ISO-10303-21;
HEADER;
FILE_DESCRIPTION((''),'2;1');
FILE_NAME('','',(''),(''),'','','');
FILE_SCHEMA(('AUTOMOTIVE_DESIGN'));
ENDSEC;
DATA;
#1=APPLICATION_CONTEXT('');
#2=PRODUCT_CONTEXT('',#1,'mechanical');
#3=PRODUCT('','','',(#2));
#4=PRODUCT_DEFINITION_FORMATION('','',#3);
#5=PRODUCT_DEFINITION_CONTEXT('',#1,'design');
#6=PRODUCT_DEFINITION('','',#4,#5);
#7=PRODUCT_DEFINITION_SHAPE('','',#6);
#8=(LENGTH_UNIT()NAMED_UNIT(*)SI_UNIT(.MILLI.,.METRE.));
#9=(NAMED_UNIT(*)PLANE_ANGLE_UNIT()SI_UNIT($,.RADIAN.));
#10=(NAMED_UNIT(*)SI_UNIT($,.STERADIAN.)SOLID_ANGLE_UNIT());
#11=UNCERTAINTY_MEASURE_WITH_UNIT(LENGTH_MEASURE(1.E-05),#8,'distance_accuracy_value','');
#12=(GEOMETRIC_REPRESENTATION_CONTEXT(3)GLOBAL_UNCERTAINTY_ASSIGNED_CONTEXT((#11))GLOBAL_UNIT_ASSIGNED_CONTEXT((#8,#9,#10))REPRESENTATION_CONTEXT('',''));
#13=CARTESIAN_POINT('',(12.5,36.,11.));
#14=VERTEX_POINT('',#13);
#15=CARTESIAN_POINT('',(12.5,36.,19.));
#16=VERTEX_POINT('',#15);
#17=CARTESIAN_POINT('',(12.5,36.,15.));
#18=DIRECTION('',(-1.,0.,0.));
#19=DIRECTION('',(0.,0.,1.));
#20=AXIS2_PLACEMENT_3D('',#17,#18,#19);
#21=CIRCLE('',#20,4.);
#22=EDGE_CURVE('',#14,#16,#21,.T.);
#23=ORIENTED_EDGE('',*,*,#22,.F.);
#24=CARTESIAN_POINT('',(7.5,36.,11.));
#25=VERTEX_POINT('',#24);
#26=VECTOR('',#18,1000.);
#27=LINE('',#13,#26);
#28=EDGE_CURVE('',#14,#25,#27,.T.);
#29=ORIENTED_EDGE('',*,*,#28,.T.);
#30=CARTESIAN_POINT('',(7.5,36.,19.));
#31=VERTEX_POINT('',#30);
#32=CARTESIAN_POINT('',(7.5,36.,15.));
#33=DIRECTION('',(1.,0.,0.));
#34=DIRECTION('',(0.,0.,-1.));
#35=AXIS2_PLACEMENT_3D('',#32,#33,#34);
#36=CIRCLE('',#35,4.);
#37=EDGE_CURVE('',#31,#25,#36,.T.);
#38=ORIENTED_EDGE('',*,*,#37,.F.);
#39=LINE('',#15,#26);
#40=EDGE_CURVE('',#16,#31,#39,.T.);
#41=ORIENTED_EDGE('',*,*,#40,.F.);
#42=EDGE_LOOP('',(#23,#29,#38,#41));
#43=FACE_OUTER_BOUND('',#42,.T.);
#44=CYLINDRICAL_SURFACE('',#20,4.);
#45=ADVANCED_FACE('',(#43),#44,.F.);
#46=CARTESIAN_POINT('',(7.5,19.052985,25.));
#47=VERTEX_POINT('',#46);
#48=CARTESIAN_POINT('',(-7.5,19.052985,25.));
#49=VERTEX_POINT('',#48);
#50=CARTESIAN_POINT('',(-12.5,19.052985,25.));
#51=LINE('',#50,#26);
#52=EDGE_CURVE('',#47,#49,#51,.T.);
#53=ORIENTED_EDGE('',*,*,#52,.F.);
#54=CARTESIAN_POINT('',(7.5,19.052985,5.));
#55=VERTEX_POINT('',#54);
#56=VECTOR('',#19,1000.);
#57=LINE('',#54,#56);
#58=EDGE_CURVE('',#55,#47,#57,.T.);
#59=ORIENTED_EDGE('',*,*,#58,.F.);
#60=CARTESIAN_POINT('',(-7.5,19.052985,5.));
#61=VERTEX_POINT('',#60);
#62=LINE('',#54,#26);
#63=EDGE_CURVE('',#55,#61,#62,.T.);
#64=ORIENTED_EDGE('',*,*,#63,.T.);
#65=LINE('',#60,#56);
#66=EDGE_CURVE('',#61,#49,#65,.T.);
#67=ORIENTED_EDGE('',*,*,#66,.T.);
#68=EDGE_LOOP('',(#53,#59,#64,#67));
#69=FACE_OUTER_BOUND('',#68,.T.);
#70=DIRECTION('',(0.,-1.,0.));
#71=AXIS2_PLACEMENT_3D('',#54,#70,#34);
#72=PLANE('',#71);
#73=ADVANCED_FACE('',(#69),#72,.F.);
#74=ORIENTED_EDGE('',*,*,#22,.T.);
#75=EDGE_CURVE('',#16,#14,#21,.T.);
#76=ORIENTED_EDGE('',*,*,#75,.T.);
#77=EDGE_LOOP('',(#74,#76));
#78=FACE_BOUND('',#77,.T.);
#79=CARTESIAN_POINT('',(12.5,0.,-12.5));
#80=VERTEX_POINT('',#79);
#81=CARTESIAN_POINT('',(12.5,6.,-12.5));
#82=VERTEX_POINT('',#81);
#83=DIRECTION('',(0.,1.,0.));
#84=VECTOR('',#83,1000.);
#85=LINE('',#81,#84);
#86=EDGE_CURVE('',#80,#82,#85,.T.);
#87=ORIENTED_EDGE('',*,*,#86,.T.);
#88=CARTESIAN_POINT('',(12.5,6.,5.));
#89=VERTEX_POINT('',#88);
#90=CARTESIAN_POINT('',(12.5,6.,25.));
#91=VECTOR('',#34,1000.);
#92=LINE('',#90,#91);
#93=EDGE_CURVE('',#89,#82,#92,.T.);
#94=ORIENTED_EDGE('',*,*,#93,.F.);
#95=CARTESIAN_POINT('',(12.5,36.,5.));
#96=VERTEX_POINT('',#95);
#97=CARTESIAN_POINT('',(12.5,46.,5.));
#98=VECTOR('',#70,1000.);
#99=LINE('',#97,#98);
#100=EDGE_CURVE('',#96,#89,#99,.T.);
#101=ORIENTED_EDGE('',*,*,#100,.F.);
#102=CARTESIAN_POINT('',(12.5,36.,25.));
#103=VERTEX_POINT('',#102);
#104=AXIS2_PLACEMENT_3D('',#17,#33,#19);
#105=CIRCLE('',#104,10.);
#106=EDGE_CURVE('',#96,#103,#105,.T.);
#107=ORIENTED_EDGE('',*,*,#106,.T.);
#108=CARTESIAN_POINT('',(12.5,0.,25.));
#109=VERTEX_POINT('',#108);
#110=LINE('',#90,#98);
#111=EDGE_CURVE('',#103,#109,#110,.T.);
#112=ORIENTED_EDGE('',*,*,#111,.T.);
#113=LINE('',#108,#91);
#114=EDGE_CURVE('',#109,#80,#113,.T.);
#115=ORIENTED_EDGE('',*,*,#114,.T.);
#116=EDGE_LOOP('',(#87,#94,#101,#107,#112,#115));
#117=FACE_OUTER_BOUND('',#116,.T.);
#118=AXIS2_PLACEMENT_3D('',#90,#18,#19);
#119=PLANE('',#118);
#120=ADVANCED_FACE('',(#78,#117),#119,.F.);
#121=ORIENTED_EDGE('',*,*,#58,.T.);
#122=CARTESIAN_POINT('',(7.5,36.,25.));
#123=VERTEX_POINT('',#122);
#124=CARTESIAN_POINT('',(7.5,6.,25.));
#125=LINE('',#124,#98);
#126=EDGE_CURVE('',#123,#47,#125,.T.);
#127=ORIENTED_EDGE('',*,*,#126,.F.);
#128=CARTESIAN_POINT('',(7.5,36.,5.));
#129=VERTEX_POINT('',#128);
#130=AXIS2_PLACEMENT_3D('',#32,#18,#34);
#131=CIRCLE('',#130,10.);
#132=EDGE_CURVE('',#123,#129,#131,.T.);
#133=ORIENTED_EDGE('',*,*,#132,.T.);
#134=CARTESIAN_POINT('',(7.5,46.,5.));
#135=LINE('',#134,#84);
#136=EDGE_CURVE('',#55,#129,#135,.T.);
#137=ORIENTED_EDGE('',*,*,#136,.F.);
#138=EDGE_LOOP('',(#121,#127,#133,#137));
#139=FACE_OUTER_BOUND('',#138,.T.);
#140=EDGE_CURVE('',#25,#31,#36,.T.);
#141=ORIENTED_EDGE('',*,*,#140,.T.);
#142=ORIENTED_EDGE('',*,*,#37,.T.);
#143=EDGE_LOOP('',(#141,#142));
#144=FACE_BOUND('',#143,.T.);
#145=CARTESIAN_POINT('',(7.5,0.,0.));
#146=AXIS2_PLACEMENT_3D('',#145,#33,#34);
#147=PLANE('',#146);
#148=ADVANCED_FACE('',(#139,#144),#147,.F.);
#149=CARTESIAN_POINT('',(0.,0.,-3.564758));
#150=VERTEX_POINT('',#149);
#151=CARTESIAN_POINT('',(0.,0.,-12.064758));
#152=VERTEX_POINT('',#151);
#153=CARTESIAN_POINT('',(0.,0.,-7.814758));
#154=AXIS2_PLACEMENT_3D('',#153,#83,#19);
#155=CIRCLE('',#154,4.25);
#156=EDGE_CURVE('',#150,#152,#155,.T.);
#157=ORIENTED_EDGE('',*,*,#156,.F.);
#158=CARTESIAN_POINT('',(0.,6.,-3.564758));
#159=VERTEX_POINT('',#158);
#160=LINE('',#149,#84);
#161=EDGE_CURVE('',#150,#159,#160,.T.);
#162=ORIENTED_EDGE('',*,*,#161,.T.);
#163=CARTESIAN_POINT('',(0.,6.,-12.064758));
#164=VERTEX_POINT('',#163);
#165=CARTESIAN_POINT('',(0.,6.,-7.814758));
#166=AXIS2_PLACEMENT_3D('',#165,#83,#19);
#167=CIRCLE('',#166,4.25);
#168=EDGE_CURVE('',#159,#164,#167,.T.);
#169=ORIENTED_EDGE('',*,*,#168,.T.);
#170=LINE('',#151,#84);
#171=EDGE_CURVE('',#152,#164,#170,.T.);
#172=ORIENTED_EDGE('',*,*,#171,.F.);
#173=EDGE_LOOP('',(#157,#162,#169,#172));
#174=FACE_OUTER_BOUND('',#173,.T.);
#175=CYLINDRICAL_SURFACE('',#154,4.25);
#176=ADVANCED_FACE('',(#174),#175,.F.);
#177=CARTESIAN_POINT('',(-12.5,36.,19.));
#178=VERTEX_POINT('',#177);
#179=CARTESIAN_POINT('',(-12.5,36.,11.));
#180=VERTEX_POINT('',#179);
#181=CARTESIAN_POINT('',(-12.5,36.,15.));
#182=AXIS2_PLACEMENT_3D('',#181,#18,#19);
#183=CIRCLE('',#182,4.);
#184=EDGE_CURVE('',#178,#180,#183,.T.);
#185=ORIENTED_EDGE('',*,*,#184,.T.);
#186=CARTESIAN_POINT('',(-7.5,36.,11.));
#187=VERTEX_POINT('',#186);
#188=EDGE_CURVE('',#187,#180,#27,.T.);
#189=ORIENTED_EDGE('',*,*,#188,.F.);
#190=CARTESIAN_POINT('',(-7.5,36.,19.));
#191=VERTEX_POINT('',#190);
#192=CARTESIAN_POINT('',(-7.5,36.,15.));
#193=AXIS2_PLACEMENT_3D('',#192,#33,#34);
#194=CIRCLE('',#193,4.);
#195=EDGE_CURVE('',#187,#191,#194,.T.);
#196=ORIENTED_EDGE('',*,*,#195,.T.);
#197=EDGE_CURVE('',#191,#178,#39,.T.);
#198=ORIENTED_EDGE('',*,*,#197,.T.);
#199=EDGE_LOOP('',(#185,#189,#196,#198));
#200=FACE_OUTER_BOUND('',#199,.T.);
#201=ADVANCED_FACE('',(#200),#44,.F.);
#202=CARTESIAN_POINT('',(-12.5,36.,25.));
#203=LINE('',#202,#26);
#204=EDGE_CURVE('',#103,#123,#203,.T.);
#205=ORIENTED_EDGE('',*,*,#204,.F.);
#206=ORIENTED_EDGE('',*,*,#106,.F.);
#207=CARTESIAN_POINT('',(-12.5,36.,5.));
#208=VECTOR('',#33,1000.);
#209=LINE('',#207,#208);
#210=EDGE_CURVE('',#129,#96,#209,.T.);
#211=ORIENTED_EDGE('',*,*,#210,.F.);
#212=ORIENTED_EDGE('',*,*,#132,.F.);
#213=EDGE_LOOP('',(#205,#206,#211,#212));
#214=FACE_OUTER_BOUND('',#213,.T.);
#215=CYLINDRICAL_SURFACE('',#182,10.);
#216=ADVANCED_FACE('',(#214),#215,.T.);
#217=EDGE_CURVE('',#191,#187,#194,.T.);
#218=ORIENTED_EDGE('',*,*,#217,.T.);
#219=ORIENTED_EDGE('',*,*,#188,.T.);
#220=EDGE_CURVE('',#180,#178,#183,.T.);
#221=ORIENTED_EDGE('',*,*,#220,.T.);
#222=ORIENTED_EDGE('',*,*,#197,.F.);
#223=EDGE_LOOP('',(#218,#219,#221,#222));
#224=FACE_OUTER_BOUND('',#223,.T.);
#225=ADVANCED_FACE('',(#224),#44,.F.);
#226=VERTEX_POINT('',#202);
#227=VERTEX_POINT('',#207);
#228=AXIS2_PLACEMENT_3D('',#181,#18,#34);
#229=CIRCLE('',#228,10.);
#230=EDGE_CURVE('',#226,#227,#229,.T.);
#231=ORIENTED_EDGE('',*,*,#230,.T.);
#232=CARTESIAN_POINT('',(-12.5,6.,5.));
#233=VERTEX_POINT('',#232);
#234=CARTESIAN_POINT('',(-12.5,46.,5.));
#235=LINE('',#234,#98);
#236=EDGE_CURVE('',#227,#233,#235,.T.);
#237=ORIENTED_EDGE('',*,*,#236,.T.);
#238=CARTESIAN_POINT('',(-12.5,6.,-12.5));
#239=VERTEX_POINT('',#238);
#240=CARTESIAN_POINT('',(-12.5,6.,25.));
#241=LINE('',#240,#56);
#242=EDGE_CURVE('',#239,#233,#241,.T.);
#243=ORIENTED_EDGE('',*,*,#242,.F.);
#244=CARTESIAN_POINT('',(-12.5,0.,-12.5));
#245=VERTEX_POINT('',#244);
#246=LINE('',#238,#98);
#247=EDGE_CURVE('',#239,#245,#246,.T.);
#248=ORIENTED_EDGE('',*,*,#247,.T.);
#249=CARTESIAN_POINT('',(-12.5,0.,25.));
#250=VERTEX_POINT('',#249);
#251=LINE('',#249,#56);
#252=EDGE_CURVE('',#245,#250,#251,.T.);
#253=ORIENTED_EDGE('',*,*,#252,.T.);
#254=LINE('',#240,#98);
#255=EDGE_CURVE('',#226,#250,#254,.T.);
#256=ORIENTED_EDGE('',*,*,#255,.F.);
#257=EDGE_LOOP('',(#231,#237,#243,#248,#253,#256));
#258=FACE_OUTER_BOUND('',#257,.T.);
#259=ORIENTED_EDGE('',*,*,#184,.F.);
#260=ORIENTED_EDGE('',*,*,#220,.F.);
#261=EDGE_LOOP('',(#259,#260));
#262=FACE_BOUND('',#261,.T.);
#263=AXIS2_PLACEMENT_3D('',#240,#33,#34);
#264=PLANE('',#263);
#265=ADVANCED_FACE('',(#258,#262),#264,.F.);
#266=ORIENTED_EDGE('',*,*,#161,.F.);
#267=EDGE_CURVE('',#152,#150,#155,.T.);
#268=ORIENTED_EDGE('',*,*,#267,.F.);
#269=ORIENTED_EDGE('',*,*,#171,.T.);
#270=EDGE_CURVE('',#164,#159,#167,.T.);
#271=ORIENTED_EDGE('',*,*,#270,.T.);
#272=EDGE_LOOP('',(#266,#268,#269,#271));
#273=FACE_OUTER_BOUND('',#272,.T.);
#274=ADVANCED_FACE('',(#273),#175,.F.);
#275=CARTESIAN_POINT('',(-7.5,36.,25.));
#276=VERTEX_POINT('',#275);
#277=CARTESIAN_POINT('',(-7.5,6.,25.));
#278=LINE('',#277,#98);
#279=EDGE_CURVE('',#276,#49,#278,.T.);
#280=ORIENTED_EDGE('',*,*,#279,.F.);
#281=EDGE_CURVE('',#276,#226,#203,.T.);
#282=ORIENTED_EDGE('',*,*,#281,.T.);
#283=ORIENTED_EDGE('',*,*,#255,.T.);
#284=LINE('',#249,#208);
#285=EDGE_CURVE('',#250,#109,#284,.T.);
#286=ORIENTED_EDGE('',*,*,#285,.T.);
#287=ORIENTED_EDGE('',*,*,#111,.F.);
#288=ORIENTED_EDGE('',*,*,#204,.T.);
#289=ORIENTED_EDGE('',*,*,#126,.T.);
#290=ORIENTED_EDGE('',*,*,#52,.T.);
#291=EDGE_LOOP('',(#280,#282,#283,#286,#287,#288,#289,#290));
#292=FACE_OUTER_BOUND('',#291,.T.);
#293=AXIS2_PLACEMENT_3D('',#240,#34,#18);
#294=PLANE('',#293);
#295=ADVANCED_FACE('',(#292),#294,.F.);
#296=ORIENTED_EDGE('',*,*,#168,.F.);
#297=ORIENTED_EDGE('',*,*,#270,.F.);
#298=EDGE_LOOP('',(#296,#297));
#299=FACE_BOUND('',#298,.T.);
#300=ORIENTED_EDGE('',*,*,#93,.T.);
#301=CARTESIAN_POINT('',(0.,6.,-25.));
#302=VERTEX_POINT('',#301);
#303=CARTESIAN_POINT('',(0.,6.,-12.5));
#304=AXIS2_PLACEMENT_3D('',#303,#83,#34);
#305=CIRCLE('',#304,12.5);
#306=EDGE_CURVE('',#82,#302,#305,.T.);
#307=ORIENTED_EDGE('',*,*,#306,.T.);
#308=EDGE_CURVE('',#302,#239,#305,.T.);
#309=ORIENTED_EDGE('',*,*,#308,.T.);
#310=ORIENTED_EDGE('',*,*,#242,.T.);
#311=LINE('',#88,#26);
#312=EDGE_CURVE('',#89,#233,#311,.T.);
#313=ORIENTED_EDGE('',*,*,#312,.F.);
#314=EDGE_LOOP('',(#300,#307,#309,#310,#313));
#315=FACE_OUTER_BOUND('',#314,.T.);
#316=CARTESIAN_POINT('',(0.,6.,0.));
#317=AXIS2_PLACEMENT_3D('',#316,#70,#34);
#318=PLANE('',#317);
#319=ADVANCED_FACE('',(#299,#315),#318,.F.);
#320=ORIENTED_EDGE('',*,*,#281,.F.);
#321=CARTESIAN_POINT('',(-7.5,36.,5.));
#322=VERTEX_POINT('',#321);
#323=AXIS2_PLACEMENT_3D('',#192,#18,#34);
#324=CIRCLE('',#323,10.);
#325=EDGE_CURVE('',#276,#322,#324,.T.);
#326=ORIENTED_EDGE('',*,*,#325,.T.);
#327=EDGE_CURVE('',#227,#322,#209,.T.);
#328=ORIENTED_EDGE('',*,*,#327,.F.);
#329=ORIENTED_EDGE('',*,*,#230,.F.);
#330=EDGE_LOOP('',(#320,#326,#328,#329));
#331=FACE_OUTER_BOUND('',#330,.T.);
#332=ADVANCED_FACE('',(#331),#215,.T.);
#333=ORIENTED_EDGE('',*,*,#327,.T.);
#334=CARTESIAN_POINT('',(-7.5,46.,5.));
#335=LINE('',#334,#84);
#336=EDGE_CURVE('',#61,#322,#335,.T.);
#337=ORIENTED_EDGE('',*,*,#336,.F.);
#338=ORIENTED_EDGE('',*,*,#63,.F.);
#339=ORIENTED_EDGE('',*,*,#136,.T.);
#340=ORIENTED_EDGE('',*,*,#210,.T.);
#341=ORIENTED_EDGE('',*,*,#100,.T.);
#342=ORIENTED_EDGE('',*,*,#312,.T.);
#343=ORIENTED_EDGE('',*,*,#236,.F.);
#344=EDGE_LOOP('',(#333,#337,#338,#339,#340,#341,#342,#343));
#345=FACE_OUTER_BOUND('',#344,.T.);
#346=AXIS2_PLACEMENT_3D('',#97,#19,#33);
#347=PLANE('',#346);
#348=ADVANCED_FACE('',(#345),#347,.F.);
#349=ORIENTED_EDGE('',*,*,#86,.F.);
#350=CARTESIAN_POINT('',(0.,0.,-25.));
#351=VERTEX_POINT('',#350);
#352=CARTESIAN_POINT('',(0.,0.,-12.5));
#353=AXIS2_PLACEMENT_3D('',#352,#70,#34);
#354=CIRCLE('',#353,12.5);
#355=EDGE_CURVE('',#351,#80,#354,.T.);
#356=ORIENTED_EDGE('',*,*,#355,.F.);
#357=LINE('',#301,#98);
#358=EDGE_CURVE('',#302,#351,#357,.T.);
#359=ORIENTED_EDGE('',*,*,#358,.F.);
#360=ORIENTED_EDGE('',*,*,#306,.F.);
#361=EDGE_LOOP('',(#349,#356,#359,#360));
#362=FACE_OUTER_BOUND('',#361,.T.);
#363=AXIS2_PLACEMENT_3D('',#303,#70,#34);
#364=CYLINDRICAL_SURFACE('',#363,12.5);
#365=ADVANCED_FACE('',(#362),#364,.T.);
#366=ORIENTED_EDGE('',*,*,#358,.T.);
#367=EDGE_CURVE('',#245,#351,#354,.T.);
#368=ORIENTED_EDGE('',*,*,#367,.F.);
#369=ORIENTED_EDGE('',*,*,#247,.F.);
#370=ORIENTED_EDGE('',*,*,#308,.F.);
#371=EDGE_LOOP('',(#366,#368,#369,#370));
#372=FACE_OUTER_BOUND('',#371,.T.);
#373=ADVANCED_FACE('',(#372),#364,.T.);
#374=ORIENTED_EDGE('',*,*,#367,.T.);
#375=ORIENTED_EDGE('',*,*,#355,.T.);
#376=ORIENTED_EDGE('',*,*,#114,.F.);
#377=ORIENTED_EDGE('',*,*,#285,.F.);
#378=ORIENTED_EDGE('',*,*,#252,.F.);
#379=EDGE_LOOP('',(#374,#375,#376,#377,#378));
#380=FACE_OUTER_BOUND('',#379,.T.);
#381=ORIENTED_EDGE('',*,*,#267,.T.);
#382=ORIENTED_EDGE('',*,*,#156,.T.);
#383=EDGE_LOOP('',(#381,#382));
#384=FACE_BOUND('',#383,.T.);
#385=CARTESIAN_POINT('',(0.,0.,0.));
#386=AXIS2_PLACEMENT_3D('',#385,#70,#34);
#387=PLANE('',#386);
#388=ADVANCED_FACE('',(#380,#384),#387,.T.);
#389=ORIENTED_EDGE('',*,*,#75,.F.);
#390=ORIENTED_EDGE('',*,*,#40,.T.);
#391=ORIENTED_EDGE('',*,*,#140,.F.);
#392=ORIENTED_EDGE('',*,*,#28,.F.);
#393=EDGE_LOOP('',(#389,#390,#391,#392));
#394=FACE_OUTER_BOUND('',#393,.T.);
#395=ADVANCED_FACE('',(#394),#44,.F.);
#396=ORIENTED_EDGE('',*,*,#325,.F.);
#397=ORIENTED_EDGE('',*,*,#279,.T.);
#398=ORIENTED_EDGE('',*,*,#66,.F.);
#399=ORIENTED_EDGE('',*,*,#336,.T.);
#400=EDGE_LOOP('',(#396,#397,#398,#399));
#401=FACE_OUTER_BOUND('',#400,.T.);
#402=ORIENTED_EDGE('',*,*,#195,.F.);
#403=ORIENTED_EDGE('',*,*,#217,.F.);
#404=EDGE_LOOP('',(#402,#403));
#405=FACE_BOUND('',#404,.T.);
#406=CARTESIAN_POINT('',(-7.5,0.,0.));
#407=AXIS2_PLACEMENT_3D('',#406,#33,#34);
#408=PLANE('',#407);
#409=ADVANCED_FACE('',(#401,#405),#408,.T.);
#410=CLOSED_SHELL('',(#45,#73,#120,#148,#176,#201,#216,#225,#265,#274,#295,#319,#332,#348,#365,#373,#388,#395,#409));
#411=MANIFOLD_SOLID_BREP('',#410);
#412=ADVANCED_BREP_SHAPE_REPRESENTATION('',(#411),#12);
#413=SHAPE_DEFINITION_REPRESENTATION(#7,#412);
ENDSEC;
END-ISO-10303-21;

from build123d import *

# Parameters (mm, degrees)
SKETCH1_W           = 25
SKETCH1_H           = 50
BOSS_EXTRUDE1_DEPTH = 6
SKETCH2_W           = 25
SKETCH2_H           = 20
BOSS_EXTRUDE2_DEPTH = 40
FILLET1_RADIUS      = 12.5
FILLET1_LENGTH      = 6
FILLET3_RADIUS      = 10
FILLET3_LENGTH      = 25
CUT_EXTRUDE1_START  = -5
SKETCH3_W           = 21.31771447
SKETCH3_H           = 40.676557725
CUT_EXTRUDE1_DEPTH  = 15
SKETCH4_R           = 4
CUT_EXTRUDE2_DEPTH  = 59.017238817
SKETCH5_R           = 4.25
CUT_EXTRUDE3_DEPTH  = 49.79805324


with BuildPart() as part:
    # Sketch1 → Boss-Extrude1 (new body)
    with BuildSketch(Plane(origin=(0, 0, 0), x_dir=(1, 0, 0), z_dir=(0, 1, 0))):
        Rectangle(SKETCH1_W, SKETCH1_H)
    extrude(amount=BOSS_EXTRUDE1_DEPTH)

    # Sketch2 → Boss-Extrude2 (add)
    with BuildSketch(Plane(origin=(0, 6, 0), x_dir=(1, 0, 0), z_dir=(0, 1, 0))):
        with Locations((0, -15)):
            Rectangle(SKETCH2_W, SKETCH2_H)
    extrude(amount=BOSS_EXTRUDE2_DEPTH)

    # Fillet1: full round fillet: the end face becomes a half cylinder, R = half its width
    fillet1_face = Plane((0, 3, -25), x_dir=(0, 1, 0), z_dir=(0, 0, -1))  # on the end face: x along it, z out of the body
    fillet1_slab = fillet1_face.offset(-FILLET1_RADIUS / 2) * Box(FILLET1_LENGTH, 2 * FILLET1_RADIUS, FILLET1_RADIUS, mode=Mode.PRIVATE)  # the body's end, R deep
    fillet1_round = Plane((0, 3, -12.5), x_dir=(0, 0, -1), z_dir=(0, 1, 0)) * Cylinder(FILLET1_RADIUS, FILLET1_LENGTH, mode=Mode.PRIVATE)  # its axis R under the face
    add(fillet1_slab - fillet1_round, mode=Mode.SUBTRACT)

    # Fillet3: full round fillet: the end face becomes a half cylinder, R = half its width
    fillet3_face = Plane((0, 46, 15), x_dir=(-1, 0, 0), z_dir=(0, 1, 0))  # on the end face: x along it, z out of the body
    fillet3_slab = fillet3_face.offset(-FILLET3_RADIUS / 2) * Box(FILLET3_LENGTH, 2 * FILLET3_RADIUS, FILLET3_RADIUS, mode=Mode.PRIVATE)  # the body's end, R deep
    fillet3_round = Plane((0, 36, 15), x_dir=(0, 1, 0), z_dir=(-1, 0, 0)) * Cylinder(FILLET3_RADIUS, FILLET3_LENGTH, mode=Mode.PRIVATE)  # its axis R under the face
    add(fillet3_slab - fillet3_round, mode=Mode.SUBTRACT)

    # Sketch3 → Cut-Extrude1 (cut)
    with BuildSketch(Plane.ZY.offset(12.5).offset(CUT_EXTRUDE1_START)):
        with Locations((15.658857235, 39.391263894)):
            Rectangle(SKETCH3_W, SKETCH3_H)
    extrude(amount=-CUT_EXTRUDE1_DEPTH, mode=Mode.SUBTRACT)

    # Sketch4 → Cut-Extrude2 (cut, through all)
    with BuildSketch(Plane.ZY.offset(12.5)):
        with Locations((15, 36)):
            Circle(SKETCH4_R)
    extrude(amount=-CUT_EXTRUDE2_DEPTH, mode=Mode.SUBTRACT)

    # Sketch5 → Cut-Extrude3 (cut, through all)
    with BuildSketch(Plane(origin=(0, 6, 0), x_dir=(1, 0, 0), z_dir=(0, 1, 0))):
        with Locations(Location((0, 7.814758418, 0), (0, 0, 270))):
            Circle(SKETCH5_R)
    extrude(amount=-CUT_EXTRUDE3_DEPTH, mode=Mode.SUBTRACT)


solid = part.part
